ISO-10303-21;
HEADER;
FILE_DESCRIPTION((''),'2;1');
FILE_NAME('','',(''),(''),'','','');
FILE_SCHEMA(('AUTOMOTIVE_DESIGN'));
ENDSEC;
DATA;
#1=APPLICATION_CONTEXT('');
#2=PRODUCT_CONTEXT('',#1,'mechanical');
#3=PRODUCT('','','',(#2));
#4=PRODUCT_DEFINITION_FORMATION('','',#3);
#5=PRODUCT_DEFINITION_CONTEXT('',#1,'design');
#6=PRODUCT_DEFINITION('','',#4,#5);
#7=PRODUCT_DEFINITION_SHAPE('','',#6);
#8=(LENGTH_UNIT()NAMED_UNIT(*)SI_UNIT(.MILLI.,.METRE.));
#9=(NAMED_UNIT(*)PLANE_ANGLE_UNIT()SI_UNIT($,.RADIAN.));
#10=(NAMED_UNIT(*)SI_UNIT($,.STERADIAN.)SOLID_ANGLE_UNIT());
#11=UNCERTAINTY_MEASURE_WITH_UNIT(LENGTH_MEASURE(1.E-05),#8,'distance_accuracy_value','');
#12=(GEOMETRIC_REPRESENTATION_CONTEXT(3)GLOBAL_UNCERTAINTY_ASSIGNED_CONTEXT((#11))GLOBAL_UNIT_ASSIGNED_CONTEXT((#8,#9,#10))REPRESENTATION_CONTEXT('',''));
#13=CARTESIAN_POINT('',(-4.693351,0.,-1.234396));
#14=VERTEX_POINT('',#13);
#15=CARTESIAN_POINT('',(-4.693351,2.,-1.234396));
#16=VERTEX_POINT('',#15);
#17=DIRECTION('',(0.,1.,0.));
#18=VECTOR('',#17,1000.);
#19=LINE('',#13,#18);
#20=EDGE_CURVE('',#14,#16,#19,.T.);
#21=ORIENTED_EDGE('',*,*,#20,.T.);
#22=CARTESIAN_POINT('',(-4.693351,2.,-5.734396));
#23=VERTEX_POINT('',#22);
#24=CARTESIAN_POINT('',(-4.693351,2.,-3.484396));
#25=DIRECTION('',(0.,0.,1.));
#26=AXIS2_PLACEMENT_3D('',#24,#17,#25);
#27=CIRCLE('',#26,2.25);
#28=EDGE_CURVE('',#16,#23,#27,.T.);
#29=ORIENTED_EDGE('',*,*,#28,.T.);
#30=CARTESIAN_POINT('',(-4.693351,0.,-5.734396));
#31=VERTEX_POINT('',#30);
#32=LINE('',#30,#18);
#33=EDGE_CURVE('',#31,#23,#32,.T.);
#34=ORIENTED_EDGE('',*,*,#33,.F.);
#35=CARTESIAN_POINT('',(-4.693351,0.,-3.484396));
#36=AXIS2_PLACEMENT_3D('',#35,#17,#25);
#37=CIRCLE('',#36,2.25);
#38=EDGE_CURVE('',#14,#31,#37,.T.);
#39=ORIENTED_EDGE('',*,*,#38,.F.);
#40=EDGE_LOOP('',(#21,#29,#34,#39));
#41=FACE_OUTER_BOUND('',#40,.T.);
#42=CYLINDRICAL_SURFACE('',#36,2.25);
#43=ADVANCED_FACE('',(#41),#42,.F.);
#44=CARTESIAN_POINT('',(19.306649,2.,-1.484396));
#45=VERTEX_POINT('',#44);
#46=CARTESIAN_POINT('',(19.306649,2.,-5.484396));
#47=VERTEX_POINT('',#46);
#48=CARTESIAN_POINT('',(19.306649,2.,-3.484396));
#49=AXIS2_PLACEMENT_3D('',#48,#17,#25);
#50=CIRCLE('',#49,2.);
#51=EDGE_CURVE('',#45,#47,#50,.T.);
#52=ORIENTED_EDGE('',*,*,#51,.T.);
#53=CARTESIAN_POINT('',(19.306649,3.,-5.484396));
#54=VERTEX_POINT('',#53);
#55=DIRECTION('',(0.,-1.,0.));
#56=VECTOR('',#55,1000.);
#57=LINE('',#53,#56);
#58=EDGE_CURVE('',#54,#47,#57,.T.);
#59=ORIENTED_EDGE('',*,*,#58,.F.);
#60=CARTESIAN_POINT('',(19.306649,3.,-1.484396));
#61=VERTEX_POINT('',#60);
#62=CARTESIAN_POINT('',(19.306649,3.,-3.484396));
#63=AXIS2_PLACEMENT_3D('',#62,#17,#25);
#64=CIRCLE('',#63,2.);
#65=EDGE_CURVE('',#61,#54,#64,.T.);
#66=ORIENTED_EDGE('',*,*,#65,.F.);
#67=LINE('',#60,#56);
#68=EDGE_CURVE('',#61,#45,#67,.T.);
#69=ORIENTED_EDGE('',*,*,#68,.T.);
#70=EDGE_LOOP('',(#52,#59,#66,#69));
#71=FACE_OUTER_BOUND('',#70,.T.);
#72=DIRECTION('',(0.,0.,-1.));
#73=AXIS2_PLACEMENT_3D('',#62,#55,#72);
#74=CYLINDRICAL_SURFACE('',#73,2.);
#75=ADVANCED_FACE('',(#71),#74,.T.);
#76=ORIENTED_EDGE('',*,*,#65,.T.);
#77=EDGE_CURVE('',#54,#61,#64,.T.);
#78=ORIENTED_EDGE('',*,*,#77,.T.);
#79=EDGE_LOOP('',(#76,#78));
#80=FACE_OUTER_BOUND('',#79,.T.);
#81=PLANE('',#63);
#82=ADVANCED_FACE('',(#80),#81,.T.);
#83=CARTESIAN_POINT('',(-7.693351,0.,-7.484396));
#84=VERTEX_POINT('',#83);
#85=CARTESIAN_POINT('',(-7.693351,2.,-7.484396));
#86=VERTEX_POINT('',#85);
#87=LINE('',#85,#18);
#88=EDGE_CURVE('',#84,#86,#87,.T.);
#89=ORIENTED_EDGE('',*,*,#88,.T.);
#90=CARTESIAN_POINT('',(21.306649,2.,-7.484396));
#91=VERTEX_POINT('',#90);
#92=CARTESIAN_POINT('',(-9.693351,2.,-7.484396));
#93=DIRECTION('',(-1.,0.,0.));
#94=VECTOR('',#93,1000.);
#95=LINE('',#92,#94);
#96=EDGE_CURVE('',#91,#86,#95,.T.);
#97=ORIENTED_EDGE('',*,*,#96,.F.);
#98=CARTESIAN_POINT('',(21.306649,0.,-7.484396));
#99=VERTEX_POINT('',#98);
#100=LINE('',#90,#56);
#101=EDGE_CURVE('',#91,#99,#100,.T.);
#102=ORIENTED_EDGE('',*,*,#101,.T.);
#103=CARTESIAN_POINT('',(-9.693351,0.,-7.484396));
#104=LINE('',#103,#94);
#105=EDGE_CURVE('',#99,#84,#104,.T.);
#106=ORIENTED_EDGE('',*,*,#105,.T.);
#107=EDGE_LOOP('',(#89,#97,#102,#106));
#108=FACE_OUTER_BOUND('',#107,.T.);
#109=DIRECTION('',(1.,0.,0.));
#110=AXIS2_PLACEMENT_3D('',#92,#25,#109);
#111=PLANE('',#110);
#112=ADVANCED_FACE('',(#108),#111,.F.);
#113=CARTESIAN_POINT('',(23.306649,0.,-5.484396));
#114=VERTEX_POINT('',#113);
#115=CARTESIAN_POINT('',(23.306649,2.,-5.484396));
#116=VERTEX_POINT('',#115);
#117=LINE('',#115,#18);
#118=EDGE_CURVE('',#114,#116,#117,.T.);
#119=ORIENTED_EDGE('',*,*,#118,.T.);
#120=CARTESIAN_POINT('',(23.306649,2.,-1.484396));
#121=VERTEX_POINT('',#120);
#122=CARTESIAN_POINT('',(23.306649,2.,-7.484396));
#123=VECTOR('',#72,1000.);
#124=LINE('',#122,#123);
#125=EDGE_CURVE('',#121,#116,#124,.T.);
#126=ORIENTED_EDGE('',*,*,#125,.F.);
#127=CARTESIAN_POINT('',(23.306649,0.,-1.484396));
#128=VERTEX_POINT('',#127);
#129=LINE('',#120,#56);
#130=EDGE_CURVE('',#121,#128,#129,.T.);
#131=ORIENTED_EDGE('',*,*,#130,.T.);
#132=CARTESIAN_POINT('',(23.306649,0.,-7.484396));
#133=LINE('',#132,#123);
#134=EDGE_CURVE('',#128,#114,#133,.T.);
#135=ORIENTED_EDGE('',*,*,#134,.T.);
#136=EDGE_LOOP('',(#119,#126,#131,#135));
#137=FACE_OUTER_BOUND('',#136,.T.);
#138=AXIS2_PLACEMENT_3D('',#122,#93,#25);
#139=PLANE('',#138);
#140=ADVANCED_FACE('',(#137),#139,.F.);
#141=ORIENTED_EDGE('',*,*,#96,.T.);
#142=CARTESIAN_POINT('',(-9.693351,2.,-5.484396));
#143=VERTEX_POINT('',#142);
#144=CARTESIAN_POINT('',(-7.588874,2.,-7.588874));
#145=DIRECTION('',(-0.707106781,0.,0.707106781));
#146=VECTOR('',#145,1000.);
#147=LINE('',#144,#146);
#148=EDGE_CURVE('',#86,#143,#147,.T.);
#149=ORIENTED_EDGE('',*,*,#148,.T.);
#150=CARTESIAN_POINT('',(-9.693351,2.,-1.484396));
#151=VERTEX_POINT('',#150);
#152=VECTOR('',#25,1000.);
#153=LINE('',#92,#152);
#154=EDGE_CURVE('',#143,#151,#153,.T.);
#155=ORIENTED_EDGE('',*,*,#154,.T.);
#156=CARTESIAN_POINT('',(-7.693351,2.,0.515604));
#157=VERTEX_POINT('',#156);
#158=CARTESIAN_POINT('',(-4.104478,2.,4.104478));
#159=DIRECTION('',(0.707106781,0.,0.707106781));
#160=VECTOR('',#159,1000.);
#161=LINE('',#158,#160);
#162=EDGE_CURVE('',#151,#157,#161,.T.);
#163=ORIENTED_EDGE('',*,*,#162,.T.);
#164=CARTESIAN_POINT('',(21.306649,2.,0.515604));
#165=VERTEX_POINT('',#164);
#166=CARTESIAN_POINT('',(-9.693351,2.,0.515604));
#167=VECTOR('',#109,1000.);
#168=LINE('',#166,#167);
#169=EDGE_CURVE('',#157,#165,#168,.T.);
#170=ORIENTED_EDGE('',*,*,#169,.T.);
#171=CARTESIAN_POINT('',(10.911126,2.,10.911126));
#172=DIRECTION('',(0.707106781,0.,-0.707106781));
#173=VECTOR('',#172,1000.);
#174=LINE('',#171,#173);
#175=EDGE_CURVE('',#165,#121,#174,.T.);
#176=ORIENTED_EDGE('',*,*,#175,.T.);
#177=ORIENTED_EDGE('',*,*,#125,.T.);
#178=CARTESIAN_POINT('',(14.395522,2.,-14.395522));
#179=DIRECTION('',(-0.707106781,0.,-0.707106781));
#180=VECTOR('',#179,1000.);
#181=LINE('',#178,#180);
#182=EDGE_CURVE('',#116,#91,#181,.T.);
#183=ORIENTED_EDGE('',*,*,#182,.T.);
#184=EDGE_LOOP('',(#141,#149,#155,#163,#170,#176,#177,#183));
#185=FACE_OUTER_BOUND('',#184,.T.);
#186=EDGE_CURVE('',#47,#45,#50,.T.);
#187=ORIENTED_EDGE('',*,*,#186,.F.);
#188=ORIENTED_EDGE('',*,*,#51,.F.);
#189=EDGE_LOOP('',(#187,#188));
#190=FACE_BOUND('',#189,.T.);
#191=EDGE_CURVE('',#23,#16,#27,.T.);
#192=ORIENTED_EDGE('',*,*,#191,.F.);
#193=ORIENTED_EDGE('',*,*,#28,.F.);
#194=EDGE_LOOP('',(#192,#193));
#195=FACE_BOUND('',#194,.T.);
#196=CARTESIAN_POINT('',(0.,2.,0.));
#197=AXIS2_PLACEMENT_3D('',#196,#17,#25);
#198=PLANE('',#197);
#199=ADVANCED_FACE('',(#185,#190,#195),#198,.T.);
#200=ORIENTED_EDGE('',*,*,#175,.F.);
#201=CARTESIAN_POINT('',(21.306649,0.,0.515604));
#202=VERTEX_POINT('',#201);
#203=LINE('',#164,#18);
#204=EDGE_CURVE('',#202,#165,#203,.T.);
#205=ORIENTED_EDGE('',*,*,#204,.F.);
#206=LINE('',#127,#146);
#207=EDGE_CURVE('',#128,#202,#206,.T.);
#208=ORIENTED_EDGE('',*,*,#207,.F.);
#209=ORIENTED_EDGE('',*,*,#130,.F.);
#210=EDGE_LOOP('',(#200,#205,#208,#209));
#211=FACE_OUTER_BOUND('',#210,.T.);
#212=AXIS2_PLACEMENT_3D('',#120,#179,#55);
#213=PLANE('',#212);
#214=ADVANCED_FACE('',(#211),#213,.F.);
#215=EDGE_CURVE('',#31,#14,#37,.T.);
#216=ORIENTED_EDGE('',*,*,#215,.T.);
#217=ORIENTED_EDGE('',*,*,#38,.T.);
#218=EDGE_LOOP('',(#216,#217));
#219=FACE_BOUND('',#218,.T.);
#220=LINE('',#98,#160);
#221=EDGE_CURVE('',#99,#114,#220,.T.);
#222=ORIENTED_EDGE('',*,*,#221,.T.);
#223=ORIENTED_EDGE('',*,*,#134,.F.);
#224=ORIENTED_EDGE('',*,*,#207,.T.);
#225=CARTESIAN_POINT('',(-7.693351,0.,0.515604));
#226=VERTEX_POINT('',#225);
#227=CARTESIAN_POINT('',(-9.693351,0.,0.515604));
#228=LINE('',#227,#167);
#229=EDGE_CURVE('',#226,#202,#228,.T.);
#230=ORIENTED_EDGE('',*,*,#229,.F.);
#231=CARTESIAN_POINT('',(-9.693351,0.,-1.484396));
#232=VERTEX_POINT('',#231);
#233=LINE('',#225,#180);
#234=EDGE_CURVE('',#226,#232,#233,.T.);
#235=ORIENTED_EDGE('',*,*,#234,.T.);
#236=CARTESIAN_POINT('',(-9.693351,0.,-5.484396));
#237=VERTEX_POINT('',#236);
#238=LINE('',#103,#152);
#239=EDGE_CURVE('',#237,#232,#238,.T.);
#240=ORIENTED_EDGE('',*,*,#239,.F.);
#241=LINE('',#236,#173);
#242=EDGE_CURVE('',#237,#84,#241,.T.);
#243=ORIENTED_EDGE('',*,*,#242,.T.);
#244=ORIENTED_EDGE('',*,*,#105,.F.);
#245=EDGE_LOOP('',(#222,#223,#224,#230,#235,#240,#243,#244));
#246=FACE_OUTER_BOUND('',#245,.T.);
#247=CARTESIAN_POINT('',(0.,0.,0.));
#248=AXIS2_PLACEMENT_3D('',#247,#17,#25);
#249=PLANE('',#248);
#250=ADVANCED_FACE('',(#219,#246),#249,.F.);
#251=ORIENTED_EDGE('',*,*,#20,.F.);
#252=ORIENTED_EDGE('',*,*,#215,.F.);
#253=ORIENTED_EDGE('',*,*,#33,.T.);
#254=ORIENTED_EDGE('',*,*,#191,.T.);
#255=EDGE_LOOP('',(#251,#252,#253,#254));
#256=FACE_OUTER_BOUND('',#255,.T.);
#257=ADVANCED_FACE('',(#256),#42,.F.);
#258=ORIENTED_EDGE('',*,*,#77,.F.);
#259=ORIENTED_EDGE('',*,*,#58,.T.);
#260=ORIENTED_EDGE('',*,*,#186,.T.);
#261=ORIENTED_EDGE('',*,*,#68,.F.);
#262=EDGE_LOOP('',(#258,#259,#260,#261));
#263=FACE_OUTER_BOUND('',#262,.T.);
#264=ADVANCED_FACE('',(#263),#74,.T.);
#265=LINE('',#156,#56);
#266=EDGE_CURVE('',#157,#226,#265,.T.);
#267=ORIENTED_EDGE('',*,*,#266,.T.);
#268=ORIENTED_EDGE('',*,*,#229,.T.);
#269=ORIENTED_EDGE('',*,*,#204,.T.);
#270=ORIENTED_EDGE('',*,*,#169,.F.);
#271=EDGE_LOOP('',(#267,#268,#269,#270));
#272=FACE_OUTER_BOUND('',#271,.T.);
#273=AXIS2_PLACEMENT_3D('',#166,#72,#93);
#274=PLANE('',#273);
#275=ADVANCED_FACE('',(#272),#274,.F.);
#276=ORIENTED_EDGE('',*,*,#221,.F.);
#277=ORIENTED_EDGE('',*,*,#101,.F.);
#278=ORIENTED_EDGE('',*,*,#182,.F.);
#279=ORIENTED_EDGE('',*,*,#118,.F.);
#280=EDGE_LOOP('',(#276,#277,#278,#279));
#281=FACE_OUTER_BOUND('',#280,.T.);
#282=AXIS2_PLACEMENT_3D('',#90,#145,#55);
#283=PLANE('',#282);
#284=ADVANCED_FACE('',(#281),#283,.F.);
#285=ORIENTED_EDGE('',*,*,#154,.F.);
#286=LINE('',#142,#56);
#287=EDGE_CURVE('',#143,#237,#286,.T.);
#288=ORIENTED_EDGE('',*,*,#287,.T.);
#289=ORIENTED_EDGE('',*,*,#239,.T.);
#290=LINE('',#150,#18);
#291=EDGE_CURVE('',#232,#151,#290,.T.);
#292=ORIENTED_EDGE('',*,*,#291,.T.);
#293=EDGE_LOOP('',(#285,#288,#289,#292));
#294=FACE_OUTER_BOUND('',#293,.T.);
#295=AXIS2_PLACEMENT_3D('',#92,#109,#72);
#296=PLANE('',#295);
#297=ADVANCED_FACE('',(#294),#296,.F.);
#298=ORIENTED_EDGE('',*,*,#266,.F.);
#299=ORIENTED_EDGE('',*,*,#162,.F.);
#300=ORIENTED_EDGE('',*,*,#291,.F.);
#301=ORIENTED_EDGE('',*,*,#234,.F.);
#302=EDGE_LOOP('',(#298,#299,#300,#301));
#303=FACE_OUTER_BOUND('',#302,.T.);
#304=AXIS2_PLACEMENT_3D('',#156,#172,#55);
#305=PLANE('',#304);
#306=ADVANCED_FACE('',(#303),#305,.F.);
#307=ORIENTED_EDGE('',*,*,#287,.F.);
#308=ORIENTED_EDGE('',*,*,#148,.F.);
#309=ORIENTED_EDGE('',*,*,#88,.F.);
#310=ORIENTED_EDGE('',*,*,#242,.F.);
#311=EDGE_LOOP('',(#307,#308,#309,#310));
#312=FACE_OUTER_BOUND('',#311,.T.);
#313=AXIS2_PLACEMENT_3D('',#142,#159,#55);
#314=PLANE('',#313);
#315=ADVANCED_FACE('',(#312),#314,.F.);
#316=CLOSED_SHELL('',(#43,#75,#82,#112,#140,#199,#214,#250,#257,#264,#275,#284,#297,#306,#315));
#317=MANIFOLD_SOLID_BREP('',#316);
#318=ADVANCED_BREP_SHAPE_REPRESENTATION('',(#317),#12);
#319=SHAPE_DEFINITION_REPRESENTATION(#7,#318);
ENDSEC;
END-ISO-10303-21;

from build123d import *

# Parameters (mm, degrees)
SKETCH1_W           = 33
SKETCH1_H           = 8
BOSS_EXTRUDE1_DEPTH = 2
SKETCH2_R           = 2.25
CUT_EXTRUDE1_DEPTH  = 25.560457127
SKETCH3_R           = 2
BOSS_EXTRUDE2_DEPTH = 1
CHAMFER2_SIZE       = 2


with BuildPart() as part:
    # Sketch1 → Boss-Extrude1 (new body)
    with BuildSketch(Plane(origin=(0, 0, 0), x_dir=(1, 0, 0), z_dir=(0, 1, 0))):
        with Locations((6.806648575, 3.484396201)):
            Rectangle(SKETCH1_W, SKETCH1_H)
    extrude(amount=BOSS_EXTRUDE1_DEPTH)

    # Sketch2 → Cut-Extrude1 (cut, through all)
    with BuildSketch(Plane(origin=(0, 2, 0), x_dir=(1, 0, 0), z_dir=(0, 1, 0))):
        with Locations(Location((-4.693351425, 3.484396201, 0), (0, 0, 270))):
            Circle(SKETCH2_R)
    extrude(amount=-CUT_EXTRUDE1_DEPTH, mode=Mode.SUBTRACT)

    # Sketch3 → Boss-Extrude2 (add)
    with BuildSketch(Plane(origin=(0, 2, 0), x_dir=(1, 0, 0), z_dir=(0, 1, 0))):
        with Locations(Location((19.306648575, 3.484396201, 0), (0, 0, 270))):
            Circle(SKETCH3_R)
    extrude(amount=BOSS_EXTRUDE2_DEPTH)

    # Chamfer2
    chamfer2_edges = [part.edges().sort_by_distance(p)[0] for p in [
        (-9.693351425, 1, -7.484396201),
        (23.306648575, 1, -7.484396201),
        (23.306648575, 1, 0.515603799),
        (-9.693351425, 1, 0.515603799),
    ]]
    chamfer(chamfer2_edges, length=CHAMFER2_SIZE)


solid = part.part
